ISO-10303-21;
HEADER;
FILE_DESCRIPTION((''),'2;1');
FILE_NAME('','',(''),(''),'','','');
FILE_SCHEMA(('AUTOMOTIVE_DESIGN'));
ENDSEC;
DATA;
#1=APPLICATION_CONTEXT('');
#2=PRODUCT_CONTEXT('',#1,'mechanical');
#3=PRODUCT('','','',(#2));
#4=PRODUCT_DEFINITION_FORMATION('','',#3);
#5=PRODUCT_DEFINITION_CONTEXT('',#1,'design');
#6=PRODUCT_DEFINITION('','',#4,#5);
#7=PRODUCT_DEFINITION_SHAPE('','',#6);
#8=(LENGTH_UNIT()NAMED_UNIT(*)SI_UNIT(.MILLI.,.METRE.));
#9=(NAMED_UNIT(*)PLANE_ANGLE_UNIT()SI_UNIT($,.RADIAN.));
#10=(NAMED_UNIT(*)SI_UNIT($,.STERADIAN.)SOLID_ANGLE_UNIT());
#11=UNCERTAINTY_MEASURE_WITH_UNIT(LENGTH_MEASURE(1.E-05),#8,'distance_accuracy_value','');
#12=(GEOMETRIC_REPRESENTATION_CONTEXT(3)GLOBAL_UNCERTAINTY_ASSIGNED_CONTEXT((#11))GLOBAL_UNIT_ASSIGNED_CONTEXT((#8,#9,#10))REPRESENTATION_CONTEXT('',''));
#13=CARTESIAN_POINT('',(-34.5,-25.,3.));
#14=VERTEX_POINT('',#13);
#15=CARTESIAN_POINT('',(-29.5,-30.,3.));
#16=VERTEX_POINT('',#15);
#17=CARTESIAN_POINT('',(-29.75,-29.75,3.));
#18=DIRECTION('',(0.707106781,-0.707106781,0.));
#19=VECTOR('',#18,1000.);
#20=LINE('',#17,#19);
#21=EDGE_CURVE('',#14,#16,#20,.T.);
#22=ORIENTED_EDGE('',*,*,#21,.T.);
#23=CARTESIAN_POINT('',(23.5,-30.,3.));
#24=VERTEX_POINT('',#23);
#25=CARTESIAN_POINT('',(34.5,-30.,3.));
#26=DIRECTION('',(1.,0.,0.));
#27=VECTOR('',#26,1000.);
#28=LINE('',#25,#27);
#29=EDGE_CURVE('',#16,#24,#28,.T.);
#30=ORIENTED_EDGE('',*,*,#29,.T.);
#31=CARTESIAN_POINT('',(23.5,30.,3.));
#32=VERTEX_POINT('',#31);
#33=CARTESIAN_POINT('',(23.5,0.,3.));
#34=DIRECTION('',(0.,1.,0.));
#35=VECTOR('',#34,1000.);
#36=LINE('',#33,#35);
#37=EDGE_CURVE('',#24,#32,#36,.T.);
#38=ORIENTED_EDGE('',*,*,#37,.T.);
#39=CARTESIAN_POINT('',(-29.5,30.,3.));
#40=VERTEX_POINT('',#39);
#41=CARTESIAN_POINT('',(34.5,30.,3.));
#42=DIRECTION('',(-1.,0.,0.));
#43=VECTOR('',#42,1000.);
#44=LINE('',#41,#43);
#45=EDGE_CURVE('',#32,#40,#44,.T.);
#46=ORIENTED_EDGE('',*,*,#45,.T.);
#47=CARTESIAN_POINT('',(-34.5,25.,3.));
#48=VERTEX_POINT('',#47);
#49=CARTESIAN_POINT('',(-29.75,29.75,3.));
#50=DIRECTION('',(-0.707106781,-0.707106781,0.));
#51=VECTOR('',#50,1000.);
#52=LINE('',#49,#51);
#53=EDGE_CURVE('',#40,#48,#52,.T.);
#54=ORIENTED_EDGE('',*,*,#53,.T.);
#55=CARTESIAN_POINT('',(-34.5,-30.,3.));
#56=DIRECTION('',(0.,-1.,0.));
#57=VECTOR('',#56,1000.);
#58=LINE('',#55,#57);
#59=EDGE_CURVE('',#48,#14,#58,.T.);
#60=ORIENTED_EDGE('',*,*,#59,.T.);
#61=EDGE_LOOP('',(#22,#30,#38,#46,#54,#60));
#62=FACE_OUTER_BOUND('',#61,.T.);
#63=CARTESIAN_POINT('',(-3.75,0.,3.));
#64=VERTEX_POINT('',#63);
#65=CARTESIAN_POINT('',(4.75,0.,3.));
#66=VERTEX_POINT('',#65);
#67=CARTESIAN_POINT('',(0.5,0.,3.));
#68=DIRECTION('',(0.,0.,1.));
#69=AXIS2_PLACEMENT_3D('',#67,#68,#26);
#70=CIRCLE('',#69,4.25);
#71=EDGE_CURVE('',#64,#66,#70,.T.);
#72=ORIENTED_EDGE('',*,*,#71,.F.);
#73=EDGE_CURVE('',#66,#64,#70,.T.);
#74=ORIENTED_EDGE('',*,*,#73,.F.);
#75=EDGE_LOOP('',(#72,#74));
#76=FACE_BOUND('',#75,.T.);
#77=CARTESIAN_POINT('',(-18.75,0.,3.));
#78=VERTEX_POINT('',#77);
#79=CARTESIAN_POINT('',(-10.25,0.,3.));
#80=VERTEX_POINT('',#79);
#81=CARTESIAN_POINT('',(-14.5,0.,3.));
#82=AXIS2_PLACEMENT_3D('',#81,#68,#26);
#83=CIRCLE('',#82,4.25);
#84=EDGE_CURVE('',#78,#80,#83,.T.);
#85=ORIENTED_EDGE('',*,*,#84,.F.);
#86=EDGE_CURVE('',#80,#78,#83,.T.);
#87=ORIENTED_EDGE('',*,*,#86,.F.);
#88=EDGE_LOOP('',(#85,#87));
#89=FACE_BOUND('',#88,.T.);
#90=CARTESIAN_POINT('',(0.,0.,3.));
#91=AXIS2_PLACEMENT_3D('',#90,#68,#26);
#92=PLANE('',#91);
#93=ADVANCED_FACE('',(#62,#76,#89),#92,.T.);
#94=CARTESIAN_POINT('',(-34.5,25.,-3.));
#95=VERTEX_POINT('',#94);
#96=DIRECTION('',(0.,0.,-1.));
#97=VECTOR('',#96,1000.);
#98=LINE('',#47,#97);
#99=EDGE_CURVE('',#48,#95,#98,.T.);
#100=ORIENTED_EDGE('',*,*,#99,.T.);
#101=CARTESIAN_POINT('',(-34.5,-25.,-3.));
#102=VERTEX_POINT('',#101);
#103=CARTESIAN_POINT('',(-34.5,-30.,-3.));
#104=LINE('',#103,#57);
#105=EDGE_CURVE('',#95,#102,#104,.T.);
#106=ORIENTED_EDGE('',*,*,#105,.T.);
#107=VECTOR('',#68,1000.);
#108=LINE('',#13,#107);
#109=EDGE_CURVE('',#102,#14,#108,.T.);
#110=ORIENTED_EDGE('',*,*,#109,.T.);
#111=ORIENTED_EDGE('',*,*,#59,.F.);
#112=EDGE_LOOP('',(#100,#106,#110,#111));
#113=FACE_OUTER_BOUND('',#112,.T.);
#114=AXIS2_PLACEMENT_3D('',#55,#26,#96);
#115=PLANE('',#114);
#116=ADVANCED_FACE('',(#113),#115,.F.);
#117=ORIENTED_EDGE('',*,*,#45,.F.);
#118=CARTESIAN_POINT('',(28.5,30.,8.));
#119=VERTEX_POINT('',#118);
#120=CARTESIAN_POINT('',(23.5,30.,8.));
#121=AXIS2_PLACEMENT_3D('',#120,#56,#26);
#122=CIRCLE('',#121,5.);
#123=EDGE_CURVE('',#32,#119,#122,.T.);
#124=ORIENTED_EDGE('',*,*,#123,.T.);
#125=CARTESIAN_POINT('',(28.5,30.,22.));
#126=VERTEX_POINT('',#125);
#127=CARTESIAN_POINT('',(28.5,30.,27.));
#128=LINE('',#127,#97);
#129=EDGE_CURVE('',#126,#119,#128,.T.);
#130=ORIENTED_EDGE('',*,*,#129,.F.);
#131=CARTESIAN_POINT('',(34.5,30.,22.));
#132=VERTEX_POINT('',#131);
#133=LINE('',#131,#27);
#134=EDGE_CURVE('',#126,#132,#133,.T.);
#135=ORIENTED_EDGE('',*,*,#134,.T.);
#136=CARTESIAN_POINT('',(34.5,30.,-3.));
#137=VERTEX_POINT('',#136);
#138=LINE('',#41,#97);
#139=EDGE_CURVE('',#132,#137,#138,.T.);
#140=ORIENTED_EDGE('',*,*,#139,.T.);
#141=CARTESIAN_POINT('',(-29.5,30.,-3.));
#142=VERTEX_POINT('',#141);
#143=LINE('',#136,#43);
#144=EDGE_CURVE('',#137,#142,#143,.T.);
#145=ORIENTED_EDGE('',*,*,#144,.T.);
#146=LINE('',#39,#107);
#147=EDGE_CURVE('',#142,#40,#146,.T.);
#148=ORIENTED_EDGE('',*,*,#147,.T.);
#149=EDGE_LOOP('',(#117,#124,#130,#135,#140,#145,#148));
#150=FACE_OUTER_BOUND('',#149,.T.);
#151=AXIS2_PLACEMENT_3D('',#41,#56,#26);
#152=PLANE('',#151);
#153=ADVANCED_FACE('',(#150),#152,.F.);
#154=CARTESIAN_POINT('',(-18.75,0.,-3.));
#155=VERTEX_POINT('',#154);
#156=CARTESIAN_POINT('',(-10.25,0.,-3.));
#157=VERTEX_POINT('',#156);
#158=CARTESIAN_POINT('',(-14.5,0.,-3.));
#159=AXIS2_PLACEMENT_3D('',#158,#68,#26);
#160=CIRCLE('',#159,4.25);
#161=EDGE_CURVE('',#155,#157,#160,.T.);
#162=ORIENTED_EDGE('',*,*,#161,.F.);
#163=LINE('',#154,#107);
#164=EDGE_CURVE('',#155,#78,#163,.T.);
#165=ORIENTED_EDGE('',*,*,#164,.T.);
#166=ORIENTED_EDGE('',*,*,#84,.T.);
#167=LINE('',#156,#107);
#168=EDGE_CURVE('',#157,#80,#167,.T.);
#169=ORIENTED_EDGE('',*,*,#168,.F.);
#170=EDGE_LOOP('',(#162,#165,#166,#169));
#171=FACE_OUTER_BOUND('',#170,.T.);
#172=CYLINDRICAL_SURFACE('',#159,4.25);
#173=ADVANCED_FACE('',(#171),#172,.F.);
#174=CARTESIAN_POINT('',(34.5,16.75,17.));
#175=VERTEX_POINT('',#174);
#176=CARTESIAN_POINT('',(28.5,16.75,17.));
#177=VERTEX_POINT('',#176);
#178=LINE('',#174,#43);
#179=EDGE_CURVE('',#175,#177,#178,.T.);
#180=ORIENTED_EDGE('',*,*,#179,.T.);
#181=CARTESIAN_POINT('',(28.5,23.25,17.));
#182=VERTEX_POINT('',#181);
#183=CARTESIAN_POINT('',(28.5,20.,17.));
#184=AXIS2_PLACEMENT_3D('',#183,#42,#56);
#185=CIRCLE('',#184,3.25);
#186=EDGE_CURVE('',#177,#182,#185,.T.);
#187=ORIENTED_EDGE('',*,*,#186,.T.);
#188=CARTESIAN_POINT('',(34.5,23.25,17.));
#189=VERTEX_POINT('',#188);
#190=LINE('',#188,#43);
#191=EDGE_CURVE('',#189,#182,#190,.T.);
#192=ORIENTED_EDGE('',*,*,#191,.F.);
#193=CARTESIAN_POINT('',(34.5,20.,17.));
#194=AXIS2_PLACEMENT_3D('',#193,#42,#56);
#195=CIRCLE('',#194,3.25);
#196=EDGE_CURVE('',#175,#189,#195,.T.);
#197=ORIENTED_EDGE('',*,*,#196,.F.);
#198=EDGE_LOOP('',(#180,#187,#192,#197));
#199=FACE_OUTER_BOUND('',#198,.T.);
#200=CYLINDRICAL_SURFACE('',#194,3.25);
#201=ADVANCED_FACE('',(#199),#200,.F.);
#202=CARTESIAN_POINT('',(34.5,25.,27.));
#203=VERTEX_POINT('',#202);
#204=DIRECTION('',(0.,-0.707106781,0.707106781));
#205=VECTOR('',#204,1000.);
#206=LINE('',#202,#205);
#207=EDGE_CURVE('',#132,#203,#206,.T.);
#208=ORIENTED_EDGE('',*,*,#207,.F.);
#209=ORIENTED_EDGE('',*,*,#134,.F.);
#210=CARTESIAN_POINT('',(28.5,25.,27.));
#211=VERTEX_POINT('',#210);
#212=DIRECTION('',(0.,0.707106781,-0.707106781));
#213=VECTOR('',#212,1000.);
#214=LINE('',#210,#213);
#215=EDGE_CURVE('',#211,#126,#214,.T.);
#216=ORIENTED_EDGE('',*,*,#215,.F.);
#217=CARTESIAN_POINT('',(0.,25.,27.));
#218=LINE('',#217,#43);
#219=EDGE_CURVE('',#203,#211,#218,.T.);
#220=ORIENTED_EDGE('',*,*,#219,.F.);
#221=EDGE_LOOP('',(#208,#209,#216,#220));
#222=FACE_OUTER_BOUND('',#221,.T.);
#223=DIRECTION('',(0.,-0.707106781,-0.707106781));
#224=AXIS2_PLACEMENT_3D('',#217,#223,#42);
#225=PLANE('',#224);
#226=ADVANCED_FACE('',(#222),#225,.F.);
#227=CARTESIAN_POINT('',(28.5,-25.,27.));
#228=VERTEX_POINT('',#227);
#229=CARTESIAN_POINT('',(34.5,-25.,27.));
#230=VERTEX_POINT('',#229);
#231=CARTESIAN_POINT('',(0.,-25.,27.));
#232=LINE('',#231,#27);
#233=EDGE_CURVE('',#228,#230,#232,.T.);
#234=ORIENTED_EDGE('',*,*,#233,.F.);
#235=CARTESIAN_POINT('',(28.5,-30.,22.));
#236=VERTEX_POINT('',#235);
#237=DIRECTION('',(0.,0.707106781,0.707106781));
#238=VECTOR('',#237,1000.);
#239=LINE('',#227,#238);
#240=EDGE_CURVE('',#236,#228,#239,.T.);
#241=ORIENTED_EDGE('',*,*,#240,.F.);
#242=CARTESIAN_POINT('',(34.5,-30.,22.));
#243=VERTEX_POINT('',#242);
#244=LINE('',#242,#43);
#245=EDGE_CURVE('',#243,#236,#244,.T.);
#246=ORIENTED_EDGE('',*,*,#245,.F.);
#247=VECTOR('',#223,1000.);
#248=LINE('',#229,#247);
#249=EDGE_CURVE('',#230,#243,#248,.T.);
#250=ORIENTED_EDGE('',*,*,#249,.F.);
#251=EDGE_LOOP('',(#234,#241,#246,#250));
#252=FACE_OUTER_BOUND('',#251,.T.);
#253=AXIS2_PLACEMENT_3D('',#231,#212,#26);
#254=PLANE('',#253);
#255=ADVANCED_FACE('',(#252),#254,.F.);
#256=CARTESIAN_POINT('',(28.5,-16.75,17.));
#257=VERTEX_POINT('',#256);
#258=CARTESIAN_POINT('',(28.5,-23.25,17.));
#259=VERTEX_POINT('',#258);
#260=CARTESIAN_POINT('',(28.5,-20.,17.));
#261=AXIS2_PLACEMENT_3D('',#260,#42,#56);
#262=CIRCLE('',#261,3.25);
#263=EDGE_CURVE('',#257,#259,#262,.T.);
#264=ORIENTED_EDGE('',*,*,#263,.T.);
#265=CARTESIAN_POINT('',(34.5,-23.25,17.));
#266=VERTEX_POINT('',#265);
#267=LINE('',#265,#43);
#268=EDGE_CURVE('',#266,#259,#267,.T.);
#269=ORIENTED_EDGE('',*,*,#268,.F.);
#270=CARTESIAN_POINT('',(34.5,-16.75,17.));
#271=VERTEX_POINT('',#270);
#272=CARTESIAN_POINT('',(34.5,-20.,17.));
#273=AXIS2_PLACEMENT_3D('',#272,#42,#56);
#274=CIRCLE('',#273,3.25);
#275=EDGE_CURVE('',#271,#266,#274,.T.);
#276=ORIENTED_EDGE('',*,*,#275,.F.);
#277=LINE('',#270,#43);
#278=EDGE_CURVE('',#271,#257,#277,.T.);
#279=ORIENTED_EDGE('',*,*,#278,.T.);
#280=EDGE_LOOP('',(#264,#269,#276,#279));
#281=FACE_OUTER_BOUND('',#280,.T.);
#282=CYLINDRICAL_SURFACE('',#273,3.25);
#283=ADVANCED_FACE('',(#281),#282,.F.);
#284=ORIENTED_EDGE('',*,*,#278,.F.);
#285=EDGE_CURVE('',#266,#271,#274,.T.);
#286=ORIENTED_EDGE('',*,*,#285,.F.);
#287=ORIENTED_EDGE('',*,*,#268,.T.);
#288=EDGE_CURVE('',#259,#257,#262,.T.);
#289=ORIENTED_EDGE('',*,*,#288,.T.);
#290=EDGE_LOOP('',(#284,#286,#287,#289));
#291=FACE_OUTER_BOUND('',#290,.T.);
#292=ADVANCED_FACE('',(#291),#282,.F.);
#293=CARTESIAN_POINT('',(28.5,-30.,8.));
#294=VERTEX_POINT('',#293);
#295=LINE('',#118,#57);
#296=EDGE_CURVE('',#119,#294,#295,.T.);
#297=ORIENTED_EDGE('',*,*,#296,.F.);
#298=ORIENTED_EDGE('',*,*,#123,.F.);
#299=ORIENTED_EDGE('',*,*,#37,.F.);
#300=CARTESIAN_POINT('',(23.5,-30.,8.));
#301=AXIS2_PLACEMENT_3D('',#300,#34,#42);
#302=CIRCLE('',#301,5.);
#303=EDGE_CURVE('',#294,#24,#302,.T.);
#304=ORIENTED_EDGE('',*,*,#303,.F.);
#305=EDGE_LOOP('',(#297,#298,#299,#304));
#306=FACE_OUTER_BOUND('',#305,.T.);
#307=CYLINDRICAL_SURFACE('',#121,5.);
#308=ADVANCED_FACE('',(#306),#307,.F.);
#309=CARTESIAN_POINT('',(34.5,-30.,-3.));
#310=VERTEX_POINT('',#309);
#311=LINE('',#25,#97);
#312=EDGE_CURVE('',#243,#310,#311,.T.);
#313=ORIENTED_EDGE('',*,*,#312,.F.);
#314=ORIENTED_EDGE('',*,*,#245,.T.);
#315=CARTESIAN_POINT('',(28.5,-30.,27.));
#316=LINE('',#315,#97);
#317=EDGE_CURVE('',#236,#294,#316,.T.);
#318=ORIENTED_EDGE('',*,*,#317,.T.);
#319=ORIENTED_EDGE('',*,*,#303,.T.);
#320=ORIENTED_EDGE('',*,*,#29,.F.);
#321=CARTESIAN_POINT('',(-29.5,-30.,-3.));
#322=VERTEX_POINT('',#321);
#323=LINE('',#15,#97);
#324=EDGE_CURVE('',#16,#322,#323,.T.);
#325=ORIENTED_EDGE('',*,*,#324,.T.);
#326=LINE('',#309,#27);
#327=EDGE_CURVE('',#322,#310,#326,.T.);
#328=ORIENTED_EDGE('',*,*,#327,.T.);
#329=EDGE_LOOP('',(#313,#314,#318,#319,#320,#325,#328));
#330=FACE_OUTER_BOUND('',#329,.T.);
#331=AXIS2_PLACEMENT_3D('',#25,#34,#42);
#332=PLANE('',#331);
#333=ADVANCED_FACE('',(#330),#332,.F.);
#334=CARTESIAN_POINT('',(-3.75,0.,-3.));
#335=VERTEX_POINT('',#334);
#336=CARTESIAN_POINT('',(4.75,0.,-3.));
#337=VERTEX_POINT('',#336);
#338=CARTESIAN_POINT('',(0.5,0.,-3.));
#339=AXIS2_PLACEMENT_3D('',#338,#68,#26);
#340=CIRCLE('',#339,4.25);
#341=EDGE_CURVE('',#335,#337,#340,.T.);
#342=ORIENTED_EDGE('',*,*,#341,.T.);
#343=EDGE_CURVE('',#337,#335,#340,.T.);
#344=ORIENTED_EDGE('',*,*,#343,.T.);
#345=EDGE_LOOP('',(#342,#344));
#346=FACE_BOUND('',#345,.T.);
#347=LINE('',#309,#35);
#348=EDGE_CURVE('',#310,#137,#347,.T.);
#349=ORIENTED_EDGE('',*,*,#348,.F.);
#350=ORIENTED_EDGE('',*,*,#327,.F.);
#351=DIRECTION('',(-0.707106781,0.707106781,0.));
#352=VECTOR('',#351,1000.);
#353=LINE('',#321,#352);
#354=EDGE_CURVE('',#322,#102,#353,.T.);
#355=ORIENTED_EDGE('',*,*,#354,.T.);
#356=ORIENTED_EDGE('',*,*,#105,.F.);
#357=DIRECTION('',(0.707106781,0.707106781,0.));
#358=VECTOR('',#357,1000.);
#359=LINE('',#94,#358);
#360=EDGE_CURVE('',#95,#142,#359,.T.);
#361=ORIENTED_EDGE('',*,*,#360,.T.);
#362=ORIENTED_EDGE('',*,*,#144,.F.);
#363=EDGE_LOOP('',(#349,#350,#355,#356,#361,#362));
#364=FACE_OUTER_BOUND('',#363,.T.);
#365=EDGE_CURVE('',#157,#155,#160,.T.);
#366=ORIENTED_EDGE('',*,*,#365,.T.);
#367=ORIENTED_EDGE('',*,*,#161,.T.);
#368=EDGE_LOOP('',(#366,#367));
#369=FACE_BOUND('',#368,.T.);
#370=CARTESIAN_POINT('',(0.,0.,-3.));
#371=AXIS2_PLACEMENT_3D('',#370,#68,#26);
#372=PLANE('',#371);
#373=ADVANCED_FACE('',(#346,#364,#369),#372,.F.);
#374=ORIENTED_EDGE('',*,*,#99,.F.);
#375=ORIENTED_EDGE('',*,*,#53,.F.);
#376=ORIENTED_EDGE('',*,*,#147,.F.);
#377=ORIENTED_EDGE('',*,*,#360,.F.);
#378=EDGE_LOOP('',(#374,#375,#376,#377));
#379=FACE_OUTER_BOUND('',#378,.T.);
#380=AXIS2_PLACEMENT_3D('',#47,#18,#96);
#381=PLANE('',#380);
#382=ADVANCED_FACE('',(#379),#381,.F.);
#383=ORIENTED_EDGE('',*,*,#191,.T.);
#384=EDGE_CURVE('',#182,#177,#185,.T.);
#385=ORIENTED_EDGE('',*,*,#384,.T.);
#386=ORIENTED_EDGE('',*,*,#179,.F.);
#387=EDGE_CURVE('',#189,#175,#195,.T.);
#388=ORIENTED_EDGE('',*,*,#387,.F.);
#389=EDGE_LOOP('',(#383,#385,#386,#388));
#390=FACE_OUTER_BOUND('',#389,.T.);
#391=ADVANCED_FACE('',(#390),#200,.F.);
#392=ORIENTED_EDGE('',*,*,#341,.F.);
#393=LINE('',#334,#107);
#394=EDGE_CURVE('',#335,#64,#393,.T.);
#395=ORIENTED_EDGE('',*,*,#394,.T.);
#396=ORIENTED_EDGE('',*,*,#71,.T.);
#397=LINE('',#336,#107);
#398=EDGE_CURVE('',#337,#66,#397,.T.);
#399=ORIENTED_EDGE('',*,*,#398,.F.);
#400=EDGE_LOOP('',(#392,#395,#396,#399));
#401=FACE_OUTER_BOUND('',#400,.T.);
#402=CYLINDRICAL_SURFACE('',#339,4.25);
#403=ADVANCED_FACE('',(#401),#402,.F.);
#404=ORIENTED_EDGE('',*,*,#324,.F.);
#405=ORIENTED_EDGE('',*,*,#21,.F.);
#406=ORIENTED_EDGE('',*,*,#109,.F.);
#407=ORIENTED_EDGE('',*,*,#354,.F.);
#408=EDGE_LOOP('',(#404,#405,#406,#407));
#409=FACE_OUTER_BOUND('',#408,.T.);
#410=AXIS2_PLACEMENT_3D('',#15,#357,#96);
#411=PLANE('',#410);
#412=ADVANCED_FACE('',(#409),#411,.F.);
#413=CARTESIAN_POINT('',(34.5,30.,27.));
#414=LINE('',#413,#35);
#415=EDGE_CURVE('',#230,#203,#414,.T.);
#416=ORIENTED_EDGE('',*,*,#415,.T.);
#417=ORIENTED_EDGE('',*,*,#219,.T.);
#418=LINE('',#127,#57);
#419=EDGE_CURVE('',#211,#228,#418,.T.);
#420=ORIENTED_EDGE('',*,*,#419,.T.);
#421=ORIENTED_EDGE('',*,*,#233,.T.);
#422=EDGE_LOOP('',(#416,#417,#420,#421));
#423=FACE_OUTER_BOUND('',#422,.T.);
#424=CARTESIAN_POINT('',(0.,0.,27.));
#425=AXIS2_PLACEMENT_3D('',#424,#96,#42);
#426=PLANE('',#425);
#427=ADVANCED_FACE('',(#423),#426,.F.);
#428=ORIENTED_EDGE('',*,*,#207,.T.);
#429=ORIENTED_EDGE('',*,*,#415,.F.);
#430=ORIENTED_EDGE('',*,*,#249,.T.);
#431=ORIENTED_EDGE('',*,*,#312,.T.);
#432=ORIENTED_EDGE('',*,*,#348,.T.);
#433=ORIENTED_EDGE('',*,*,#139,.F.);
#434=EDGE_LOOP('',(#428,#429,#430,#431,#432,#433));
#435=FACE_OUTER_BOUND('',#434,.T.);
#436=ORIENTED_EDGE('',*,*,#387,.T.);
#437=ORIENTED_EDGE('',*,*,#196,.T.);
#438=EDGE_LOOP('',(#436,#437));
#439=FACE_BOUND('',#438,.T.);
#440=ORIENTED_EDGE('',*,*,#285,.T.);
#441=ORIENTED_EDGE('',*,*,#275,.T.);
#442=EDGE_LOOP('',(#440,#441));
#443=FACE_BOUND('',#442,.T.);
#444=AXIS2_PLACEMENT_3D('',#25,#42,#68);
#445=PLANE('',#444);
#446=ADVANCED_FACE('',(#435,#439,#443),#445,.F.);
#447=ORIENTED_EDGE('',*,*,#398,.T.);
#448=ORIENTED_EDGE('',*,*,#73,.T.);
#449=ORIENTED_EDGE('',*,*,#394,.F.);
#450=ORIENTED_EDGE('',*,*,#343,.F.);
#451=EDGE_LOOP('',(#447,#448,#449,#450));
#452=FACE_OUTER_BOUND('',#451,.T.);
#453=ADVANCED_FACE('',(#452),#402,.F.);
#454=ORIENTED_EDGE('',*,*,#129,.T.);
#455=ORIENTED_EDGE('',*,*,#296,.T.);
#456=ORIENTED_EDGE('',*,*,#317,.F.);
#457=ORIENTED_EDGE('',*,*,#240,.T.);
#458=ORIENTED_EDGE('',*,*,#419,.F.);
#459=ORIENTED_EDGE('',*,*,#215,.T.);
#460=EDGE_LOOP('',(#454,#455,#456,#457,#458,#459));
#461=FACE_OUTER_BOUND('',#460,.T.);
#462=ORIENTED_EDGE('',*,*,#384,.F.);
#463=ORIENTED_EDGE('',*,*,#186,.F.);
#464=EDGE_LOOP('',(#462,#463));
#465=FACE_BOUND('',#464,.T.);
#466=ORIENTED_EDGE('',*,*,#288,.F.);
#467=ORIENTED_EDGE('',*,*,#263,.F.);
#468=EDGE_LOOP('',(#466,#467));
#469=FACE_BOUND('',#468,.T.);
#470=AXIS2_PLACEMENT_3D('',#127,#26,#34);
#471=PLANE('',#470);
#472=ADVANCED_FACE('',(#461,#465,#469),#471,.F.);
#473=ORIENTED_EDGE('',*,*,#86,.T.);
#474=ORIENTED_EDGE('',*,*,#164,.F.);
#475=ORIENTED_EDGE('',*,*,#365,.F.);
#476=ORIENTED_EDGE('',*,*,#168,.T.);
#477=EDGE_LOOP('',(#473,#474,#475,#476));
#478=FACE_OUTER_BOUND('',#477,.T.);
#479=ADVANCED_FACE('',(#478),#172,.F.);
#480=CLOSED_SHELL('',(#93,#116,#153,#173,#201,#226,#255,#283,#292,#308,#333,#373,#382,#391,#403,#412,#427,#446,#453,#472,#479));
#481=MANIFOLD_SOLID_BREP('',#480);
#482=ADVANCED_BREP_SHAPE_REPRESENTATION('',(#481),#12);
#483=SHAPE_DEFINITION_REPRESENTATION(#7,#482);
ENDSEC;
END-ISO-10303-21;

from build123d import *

# Parameters (mm, degrees)
SKETCH1_W           = 69
SKETCH1_H           = 60
BOSS_EXTRUDE1_DEPTH = 3
SKETCH2_W           = 6
SKETCH2_H           = 60
BOSS_EXTRUDE2_DEPTH = 24
CHAMFER1_SIZE       = 5
SKETCH3_R           = 4.25
CUT_EXTRUDE1_DEPTH  = 52.635743434
FILLET1_R           = 5
SKETCH4_R           = 3.25
CUT_EXTRUDE2_DEPTH  = 75.81978348


with BuildPart() as part:
    # Sketch1 → Boss-Extrude1 (new, symmetric)
    with BuildSketch(Plane.XY):
        Rectangle(SKETCH1_W, SKETCH1_H)
    extrude(amount=BOSS_EXTRUDE1_DEPTH, both=True)

    # Sketch2 → Boss-Extrude2 (add)
    with BuildSketch(Plane.XY.offset(3)):
        with Locations((31.5, 0)):
            Rectangle(SKETCH2_W, SKETCH2_H)
    extrude(amount=BOSS_EXTRUDE2_DEPTH)

    # Chamfer1
    chamfer1_edges = [part.edges().sort_by_distance(p)[0] for p in [
        (31.5, 30, 27),
        (31.5, -30, 27),
        (-34.5, 30, 0),
        (-34.5, -30, 0),
    ]]
    chamfer(chamfer1_edges, length=CHAMFER1_SIZE)

    # Sketch3 → Cut-Extrude1 (cut, through all)
    with BuildSketch(Plane.XY.offset(3)):
        with Locations((-14.5, 0)):
            Circle(SKETCH3_R)
        with Locations((0.5, 0)):
            Circle(SKETCH3_R)
    extrude(amount=-CUT_EXTRUDE1_DEPTH, mode=Mode.SUBTRACT)

    # Fillet1
    fillet1_edges = [part.edges().sort_by_distance(p)[0] for p in [
        (28.5, 0, 3),
    ]]
    fillet(fillet1_edges, radius=FILLET1_R)

    # Sketch4 → Cut-Extrude2 (cut, through all)
    with BuildSketch(Plane.ZY.offset(-28.5)):
        with Locations(Location((17, 20, 0), (0, 0, 270))):
            Circle(SKETCH4_R)
        with Locations(Location((17, -20, 0), (0, 0, 270))):
            Circle(SKETCH4_R)
    extrude(amount=-CUT_EXTRUDE2_DEPTH, mode=Mode.SUBTRACT)


solid = part.part
